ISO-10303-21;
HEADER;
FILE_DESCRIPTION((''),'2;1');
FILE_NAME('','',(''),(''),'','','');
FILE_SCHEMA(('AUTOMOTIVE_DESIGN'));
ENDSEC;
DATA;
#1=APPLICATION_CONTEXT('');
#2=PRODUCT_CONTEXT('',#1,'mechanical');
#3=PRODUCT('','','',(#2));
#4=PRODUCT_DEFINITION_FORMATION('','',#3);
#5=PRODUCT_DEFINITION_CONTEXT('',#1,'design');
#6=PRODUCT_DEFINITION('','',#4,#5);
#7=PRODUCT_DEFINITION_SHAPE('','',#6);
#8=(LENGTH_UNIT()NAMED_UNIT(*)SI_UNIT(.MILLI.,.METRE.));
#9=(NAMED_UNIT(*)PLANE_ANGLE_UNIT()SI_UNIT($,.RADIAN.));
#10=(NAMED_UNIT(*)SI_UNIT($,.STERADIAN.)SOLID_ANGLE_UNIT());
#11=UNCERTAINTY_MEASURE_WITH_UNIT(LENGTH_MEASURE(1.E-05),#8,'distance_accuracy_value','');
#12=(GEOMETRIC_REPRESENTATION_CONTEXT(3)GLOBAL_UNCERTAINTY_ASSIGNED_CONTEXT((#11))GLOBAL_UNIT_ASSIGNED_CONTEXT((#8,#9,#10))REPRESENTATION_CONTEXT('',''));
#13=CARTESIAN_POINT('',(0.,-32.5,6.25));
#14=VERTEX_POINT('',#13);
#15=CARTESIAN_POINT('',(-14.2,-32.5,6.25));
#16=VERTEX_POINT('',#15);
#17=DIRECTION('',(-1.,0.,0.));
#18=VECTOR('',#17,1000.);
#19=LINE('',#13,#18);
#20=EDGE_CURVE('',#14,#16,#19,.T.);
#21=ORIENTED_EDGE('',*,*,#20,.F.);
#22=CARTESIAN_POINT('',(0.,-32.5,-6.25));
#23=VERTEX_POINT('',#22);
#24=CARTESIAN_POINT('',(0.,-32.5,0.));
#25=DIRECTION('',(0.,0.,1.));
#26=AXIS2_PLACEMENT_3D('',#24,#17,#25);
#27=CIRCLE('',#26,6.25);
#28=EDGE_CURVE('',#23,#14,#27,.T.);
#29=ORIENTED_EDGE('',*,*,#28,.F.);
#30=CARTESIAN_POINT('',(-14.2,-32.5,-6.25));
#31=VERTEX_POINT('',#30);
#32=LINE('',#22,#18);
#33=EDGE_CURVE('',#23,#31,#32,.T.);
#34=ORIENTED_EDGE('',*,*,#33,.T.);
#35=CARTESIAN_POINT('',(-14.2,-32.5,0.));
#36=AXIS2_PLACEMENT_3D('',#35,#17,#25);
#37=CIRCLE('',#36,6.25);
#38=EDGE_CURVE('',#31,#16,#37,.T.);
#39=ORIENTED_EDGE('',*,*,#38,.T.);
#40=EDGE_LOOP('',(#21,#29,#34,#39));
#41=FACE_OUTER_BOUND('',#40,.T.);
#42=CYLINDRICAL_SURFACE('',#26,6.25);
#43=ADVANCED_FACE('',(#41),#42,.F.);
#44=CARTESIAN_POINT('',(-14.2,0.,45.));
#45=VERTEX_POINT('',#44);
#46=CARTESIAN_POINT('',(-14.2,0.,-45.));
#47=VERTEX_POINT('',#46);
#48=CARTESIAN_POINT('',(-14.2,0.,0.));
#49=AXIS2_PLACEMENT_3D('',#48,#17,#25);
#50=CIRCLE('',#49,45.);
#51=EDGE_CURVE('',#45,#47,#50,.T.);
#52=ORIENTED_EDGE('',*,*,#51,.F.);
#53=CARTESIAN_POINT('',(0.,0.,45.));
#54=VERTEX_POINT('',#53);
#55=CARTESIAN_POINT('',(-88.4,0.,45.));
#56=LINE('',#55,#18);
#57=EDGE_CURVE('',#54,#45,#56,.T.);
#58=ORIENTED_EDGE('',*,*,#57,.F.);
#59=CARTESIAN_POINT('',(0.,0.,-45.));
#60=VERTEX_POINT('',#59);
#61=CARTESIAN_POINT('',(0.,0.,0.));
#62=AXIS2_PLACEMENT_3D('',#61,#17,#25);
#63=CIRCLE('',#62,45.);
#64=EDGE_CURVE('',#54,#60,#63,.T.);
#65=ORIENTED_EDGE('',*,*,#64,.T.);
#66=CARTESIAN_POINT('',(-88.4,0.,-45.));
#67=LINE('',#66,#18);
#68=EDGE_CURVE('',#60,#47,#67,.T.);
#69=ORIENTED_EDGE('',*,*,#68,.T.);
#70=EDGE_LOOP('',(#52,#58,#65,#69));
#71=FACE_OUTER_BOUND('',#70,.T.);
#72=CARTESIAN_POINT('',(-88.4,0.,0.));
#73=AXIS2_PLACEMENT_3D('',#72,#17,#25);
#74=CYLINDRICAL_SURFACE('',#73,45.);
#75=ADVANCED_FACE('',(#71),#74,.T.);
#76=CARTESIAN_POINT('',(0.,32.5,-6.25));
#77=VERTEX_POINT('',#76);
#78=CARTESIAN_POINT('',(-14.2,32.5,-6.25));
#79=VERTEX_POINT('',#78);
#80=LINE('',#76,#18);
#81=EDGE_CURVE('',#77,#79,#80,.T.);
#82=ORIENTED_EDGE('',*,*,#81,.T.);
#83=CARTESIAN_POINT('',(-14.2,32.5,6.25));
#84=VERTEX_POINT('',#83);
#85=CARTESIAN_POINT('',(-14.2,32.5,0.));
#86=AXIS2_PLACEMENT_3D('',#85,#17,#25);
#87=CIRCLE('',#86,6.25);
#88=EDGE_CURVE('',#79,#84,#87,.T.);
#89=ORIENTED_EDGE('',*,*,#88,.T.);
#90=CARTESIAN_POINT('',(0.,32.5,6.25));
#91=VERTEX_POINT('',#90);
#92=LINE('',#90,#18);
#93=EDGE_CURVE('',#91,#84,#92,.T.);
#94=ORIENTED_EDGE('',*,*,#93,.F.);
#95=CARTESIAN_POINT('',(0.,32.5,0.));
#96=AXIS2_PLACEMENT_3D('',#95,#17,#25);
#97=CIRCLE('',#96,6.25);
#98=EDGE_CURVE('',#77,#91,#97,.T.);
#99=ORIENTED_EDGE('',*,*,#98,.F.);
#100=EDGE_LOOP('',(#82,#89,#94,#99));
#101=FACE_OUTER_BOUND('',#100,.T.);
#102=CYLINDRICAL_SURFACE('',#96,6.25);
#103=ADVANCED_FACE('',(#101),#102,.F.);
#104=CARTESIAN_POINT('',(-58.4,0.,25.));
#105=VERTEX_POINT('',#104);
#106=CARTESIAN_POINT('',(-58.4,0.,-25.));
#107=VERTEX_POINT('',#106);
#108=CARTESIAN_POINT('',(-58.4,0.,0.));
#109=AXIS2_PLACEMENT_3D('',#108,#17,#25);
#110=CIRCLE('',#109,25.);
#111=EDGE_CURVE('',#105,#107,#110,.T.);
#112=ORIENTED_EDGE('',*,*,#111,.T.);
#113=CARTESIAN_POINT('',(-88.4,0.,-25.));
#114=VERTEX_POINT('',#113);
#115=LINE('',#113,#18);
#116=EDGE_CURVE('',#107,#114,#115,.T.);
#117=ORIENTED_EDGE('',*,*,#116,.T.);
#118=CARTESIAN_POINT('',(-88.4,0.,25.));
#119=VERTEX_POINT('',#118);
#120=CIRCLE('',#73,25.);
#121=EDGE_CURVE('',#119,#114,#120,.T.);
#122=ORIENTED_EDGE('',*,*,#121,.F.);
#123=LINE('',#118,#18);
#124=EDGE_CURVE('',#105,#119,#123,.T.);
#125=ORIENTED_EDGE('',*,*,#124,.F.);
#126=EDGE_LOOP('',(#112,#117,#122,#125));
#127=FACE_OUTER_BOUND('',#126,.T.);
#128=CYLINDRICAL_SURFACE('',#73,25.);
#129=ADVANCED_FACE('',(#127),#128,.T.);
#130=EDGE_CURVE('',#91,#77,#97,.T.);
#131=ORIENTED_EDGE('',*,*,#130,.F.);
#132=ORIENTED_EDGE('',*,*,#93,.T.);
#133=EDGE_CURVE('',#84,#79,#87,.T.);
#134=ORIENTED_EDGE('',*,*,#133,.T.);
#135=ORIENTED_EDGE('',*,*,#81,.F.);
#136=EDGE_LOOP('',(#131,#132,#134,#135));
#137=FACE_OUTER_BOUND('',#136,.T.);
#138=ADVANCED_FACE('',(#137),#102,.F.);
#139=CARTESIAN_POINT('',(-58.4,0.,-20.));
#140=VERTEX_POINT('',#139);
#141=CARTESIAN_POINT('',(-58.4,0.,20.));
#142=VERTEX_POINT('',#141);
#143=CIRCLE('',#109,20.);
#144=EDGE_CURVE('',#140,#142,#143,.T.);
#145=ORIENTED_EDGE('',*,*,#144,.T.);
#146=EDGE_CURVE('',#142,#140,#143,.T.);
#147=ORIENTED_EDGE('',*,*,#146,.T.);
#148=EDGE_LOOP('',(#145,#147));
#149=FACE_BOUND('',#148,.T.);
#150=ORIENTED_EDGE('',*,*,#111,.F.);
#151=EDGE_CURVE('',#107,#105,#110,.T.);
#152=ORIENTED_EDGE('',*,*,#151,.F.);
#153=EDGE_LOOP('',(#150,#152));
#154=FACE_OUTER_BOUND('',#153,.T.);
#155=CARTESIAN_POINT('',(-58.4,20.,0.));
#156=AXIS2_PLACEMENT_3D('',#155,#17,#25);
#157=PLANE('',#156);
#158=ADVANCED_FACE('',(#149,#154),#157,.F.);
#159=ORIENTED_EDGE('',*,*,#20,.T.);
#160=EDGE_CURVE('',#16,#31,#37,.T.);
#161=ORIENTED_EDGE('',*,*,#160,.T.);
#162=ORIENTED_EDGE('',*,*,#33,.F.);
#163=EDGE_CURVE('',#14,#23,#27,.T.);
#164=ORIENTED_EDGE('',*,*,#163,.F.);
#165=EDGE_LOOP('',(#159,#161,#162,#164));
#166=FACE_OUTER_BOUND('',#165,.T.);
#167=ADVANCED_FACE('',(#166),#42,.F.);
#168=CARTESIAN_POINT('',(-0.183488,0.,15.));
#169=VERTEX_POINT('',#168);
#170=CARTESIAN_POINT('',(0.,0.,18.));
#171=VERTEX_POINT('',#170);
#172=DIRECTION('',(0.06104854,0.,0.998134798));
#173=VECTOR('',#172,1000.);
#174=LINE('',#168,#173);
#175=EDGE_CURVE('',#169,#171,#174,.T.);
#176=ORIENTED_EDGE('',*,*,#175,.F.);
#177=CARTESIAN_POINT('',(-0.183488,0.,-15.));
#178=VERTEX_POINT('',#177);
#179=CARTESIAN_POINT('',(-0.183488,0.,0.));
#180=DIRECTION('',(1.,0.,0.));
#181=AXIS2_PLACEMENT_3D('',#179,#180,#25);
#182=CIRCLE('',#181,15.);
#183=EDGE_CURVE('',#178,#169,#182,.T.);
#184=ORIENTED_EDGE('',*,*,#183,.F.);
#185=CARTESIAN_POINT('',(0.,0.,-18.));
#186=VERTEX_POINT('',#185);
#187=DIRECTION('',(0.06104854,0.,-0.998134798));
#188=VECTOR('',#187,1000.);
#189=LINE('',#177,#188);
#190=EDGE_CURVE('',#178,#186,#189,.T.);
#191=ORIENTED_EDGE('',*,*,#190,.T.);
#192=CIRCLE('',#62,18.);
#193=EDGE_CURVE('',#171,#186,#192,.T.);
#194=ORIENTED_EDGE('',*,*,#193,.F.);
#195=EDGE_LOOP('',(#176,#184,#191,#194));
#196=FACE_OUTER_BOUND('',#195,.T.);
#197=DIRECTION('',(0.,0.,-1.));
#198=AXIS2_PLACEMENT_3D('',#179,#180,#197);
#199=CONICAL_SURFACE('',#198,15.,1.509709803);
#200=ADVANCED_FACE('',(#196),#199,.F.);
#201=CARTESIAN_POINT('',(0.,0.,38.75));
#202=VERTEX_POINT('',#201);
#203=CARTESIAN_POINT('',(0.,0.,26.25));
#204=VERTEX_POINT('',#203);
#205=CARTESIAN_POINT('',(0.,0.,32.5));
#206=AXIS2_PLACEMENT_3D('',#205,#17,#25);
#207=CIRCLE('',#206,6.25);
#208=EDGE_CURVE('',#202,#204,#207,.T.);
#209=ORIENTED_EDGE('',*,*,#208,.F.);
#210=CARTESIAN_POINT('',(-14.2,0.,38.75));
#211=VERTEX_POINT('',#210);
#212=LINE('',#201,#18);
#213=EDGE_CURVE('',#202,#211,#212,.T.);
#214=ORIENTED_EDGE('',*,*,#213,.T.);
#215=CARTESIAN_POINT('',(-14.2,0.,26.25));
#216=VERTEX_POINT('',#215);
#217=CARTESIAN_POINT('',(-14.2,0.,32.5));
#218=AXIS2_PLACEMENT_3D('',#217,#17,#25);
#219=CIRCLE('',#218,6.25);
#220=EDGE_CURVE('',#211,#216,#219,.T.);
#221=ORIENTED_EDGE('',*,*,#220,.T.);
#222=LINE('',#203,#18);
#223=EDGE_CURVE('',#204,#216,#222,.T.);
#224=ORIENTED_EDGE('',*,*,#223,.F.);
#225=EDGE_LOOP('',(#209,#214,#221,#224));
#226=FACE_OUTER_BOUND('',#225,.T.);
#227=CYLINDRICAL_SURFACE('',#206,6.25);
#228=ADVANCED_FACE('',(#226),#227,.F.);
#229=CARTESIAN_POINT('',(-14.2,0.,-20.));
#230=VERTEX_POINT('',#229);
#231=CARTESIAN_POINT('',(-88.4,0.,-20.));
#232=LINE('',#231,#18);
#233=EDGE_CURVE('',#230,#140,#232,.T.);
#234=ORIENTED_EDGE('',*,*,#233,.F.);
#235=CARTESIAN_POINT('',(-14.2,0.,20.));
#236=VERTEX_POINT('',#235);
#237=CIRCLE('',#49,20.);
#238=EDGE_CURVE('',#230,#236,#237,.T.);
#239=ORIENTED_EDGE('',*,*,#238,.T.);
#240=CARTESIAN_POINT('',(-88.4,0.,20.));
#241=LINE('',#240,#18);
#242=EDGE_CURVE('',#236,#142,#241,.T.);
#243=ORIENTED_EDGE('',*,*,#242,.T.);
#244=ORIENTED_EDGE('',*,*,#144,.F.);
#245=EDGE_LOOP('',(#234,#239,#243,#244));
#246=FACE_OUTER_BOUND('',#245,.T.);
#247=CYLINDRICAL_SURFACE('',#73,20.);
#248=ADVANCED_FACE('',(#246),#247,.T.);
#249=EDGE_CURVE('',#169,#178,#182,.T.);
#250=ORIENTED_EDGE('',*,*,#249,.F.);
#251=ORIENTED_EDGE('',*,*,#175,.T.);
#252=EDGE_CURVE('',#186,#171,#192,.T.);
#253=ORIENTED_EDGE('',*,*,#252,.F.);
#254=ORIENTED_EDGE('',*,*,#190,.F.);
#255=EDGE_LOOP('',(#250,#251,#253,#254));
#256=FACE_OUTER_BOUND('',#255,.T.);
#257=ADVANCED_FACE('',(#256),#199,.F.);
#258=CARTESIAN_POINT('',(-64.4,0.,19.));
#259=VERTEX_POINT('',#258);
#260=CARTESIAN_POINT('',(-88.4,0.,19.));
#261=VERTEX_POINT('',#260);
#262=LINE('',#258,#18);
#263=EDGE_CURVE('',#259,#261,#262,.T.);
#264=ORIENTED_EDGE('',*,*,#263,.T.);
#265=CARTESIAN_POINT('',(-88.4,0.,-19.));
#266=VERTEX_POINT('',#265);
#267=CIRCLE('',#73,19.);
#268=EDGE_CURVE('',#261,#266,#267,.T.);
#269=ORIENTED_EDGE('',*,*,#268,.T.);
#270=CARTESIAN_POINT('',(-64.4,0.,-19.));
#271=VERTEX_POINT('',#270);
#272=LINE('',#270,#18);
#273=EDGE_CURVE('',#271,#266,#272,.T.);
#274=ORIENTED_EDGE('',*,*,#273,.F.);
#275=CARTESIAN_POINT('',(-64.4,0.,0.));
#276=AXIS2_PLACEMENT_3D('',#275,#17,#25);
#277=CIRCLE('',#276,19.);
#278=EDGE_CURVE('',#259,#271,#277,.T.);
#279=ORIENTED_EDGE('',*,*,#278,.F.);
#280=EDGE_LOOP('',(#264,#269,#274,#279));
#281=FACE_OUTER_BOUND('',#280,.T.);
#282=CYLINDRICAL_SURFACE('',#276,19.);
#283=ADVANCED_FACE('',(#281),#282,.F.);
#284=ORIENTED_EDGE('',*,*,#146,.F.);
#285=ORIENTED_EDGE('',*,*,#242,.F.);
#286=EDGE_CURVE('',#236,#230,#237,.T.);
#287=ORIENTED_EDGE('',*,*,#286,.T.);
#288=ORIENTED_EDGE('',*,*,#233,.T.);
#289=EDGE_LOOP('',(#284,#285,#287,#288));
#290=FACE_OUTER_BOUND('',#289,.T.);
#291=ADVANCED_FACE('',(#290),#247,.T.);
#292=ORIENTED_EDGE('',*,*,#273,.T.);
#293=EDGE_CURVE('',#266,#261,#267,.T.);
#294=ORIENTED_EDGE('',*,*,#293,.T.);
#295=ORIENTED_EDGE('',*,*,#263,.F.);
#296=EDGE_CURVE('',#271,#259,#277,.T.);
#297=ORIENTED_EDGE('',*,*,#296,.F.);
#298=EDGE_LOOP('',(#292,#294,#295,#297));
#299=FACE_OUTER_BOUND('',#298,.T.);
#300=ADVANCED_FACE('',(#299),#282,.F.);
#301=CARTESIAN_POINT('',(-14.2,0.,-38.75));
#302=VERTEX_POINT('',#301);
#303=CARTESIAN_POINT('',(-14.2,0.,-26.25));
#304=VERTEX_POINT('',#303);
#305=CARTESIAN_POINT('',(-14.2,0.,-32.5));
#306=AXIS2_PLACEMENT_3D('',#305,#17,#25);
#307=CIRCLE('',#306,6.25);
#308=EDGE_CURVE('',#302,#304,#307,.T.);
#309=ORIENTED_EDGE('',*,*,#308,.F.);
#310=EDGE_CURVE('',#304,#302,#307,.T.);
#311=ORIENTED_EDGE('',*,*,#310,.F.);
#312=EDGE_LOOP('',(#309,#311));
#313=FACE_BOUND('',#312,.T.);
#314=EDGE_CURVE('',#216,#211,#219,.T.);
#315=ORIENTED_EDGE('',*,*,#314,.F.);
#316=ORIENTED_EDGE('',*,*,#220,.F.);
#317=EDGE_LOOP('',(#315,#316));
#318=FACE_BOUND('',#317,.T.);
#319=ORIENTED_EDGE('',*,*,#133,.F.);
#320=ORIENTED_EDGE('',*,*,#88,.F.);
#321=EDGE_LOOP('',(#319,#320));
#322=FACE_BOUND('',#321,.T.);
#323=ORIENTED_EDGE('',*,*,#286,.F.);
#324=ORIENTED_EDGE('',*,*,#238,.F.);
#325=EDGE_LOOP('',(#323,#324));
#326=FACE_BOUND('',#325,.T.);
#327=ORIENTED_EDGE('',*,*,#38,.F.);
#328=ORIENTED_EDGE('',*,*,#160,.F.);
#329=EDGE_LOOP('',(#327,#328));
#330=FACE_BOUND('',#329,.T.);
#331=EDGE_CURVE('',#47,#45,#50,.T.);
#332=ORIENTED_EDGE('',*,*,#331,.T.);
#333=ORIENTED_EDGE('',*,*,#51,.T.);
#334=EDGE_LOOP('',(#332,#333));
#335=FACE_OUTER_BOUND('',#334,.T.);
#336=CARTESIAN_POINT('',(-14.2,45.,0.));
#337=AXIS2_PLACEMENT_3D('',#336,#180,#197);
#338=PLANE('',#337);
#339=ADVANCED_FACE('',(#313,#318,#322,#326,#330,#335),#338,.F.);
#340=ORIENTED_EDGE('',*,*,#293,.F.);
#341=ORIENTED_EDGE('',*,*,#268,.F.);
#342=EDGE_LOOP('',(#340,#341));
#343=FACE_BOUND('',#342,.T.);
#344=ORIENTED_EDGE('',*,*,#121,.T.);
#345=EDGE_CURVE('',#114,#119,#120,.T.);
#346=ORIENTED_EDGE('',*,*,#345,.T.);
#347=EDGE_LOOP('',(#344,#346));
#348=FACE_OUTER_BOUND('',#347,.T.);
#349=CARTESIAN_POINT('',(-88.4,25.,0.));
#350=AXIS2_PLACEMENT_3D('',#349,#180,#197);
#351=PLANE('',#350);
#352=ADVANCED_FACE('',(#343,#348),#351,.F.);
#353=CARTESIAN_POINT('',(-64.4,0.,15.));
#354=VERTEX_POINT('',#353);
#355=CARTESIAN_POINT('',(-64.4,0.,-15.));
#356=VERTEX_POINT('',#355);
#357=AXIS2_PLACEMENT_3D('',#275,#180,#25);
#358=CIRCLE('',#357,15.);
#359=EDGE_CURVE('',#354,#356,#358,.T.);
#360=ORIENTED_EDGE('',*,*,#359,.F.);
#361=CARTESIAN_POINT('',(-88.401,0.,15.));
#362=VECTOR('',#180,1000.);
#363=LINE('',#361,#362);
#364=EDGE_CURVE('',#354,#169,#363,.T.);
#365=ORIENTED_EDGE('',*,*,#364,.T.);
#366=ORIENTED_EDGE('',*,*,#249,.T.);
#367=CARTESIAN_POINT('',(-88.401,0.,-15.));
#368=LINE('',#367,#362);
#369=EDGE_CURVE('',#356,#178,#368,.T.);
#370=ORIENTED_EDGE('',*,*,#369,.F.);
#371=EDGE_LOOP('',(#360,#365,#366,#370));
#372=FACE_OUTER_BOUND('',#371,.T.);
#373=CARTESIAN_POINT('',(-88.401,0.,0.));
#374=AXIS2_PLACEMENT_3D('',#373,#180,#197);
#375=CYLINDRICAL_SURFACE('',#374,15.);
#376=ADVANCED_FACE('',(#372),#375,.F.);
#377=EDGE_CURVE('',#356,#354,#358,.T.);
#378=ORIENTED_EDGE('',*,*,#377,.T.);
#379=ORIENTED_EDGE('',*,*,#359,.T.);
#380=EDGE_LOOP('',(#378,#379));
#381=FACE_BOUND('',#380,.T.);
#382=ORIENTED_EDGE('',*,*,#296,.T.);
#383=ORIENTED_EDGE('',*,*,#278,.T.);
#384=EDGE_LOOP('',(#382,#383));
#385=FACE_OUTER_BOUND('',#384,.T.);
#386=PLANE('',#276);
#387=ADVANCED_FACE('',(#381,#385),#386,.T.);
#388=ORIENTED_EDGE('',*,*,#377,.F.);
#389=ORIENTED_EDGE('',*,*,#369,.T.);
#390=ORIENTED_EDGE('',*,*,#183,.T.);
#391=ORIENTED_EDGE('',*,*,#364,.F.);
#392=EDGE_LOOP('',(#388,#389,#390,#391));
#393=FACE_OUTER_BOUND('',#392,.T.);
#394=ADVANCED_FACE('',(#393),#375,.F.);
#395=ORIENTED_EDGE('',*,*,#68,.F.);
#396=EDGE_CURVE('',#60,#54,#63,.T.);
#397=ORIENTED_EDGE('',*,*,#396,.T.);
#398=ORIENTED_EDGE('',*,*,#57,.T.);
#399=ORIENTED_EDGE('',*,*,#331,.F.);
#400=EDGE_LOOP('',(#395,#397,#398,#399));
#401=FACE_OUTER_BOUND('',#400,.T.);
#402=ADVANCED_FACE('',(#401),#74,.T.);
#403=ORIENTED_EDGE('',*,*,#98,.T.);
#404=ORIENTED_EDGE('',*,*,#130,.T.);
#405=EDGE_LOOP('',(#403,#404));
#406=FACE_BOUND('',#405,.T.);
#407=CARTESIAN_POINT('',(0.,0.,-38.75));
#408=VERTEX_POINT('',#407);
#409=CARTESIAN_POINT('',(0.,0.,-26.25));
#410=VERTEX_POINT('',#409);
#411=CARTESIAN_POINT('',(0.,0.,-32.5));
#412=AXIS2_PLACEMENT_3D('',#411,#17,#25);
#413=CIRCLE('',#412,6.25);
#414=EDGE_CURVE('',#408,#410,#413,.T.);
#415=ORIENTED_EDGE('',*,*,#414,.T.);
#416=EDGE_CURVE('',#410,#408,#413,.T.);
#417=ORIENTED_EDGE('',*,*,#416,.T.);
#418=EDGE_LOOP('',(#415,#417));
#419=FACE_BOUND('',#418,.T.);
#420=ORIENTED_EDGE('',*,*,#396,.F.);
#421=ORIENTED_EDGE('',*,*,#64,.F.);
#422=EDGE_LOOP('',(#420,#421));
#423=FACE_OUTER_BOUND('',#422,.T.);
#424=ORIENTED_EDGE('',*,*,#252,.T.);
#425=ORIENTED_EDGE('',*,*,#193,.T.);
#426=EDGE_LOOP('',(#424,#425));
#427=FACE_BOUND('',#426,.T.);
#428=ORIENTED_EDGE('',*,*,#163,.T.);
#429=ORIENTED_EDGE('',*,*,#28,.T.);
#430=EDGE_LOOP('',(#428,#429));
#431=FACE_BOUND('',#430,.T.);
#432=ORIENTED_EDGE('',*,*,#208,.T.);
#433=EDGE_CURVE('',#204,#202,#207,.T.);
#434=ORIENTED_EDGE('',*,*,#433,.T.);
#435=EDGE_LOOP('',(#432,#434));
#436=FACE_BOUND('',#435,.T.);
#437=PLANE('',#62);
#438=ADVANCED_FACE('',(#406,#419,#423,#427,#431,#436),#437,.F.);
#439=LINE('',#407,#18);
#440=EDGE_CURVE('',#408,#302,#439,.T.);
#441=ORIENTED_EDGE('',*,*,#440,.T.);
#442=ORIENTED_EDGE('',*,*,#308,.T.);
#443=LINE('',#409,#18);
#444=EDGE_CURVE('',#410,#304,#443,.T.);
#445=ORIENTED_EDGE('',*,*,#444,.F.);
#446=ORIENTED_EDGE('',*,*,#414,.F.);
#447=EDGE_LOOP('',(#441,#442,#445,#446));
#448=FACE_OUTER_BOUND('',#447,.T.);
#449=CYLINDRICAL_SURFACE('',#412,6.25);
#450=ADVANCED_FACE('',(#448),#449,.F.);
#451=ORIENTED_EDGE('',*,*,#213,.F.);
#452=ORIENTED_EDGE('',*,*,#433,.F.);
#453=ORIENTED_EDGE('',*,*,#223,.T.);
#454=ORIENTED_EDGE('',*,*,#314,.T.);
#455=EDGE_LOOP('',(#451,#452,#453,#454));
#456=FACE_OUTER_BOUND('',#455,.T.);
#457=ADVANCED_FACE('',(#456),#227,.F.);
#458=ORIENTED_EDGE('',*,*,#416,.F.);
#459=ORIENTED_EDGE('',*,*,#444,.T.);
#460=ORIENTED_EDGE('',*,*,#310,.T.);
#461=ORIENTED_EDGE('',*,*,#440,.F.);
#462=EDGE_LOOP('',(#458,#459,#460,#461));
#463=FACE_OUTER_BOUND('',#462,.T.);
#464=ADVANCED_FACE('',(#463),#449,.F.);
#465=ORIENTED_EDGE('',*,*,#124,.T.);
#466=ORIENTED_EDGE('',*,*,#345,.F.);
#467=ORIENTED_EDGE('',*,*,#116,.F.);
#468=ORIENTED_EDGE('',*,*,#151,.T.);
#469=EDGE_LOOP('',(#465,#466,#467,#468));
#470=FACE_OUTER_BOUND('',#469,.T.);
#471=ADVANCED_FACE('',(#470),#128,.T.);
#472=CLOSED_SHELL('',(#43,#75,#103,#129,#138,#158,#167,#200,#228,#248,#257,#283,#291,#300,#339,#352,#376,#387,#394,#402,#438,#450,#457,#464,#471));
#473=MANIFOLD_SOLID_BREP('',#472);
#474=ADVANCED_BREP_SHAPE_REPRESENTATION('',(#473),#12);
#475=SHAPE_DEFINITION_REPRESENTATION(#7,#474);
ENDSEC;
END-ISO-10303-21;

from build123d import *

# Parameters (mm, degrees)
BOLT_HOLES_SKETCH_R             = 6.25
FLANGE_BOLT_HOLES_4X_12_5_DEPTH = 98.75295392
COUNTERBORE_SKETCH_R            = 19
COUNTERBORE_38X24_DEPTH         = 24
THROUGH_BORE_30_REACH           = 110.925
THROUGH_BORE_SKETCH_R           = 15
BORE_CHAMFER_3MM_SIZE           = 3
BORE_CHAMFER_3MM_SIZE2          = 0.18348786


with BuildPart() as part:
    # Sleeve Profile Sketch → Flanged Sleeve Body (revolve)
    with BuildSketch(Plane.XY, mode=Mode.PRIVATE) as flanged_sleeve_body_sk:
        Polygon((0, 0), (0, 45), (-14.2, 45), (-14.2, 20), (-58.4, 20), (-58.4, 25), (-88.4, 25), (-88.4, 0), align=None)
    revolve(flanged_sleeve_body_sk.sketch.rotate(Axis((-88.4, 0, 0), (1, 0, 0)), 90), axis=Axis((-88.4, 0, 0), (1, 0, 0)))

    # Bolt Holes Sketch → Flange Bolt Holes 4xØ12.5 (cut, through all)
    with BuildSketch(Plane.ZY.offset(14.2)):
        with Locations((0, -32.5)):
            Circle(BOLT_HOLES_SKETCH_R)
        with Locations((-32.5, 0)):
            Circle(BOLT_HOLES_SKETCH_R)
        with Locations((0, 32.5)):
            Circle(BOLT_HOLES_SKETCH_R)
        with Locations((32.5, 0)):
            Circle(BOLT_HOLES_SKETCH_R)
    extrude(amount=-FLANGE_BOLT_HOLES_4X_12_5_DEPTH, mode=Mode.SUBTRACT)

    # Counterbore Sketch → Counterbore Ø38x24 (cut)
    with BuildSketch(Plane.ZY.offset(88.4)):
        Circle(COUNTERBORE_SKETCH_R)
    extrude(amount=-COUNTERBORE_38X24_DEPTH, mode=Mode.SUBTRACT)

    # Through Bore Sketch → Through Bore Ø30 (cut, up to next)
    with BuildSketch(Plane(origin=(0, 0, 0), x_dir=(0, 0, -1), z_dir=(1, 0, 0)), mode=Mode.PRIVATE) as through_bore_30_sk1:
        Circle(THROUGH_BORE_SKETCH_R)
    through_bore_30_tool1 = extrude(through_bore_30_sk1.sketch, amount=-THROUGH_BORE_30_REACH, mode=Mode.PRIVATE) & part.part
    add(through_bore_30_tool1.solids().sort_by_distance((0, 0, 0))[0], mode=Mode.SUBTRACT)

    # Bore Chamfer 3mm
    bore_chamfer_3mm_edges = [part.edges().sort_by_distance(p)[0] for p in [
        (0, 0, 15),
    ]]
    bore_chamfer_3mm_side = [part.faces().sort_by_distance(p)[0] for p in [
        (0, 0, -43.727207794),
    ]]
    chamfer(bore_chamfer_3mm_edges, length=BORE_CHAMFER_3MM_SIZE, length2=BORE_CHAMFER_3MM_SIZE2, reference=bore_chamfer_3mm_side[0])


solid = part.part
